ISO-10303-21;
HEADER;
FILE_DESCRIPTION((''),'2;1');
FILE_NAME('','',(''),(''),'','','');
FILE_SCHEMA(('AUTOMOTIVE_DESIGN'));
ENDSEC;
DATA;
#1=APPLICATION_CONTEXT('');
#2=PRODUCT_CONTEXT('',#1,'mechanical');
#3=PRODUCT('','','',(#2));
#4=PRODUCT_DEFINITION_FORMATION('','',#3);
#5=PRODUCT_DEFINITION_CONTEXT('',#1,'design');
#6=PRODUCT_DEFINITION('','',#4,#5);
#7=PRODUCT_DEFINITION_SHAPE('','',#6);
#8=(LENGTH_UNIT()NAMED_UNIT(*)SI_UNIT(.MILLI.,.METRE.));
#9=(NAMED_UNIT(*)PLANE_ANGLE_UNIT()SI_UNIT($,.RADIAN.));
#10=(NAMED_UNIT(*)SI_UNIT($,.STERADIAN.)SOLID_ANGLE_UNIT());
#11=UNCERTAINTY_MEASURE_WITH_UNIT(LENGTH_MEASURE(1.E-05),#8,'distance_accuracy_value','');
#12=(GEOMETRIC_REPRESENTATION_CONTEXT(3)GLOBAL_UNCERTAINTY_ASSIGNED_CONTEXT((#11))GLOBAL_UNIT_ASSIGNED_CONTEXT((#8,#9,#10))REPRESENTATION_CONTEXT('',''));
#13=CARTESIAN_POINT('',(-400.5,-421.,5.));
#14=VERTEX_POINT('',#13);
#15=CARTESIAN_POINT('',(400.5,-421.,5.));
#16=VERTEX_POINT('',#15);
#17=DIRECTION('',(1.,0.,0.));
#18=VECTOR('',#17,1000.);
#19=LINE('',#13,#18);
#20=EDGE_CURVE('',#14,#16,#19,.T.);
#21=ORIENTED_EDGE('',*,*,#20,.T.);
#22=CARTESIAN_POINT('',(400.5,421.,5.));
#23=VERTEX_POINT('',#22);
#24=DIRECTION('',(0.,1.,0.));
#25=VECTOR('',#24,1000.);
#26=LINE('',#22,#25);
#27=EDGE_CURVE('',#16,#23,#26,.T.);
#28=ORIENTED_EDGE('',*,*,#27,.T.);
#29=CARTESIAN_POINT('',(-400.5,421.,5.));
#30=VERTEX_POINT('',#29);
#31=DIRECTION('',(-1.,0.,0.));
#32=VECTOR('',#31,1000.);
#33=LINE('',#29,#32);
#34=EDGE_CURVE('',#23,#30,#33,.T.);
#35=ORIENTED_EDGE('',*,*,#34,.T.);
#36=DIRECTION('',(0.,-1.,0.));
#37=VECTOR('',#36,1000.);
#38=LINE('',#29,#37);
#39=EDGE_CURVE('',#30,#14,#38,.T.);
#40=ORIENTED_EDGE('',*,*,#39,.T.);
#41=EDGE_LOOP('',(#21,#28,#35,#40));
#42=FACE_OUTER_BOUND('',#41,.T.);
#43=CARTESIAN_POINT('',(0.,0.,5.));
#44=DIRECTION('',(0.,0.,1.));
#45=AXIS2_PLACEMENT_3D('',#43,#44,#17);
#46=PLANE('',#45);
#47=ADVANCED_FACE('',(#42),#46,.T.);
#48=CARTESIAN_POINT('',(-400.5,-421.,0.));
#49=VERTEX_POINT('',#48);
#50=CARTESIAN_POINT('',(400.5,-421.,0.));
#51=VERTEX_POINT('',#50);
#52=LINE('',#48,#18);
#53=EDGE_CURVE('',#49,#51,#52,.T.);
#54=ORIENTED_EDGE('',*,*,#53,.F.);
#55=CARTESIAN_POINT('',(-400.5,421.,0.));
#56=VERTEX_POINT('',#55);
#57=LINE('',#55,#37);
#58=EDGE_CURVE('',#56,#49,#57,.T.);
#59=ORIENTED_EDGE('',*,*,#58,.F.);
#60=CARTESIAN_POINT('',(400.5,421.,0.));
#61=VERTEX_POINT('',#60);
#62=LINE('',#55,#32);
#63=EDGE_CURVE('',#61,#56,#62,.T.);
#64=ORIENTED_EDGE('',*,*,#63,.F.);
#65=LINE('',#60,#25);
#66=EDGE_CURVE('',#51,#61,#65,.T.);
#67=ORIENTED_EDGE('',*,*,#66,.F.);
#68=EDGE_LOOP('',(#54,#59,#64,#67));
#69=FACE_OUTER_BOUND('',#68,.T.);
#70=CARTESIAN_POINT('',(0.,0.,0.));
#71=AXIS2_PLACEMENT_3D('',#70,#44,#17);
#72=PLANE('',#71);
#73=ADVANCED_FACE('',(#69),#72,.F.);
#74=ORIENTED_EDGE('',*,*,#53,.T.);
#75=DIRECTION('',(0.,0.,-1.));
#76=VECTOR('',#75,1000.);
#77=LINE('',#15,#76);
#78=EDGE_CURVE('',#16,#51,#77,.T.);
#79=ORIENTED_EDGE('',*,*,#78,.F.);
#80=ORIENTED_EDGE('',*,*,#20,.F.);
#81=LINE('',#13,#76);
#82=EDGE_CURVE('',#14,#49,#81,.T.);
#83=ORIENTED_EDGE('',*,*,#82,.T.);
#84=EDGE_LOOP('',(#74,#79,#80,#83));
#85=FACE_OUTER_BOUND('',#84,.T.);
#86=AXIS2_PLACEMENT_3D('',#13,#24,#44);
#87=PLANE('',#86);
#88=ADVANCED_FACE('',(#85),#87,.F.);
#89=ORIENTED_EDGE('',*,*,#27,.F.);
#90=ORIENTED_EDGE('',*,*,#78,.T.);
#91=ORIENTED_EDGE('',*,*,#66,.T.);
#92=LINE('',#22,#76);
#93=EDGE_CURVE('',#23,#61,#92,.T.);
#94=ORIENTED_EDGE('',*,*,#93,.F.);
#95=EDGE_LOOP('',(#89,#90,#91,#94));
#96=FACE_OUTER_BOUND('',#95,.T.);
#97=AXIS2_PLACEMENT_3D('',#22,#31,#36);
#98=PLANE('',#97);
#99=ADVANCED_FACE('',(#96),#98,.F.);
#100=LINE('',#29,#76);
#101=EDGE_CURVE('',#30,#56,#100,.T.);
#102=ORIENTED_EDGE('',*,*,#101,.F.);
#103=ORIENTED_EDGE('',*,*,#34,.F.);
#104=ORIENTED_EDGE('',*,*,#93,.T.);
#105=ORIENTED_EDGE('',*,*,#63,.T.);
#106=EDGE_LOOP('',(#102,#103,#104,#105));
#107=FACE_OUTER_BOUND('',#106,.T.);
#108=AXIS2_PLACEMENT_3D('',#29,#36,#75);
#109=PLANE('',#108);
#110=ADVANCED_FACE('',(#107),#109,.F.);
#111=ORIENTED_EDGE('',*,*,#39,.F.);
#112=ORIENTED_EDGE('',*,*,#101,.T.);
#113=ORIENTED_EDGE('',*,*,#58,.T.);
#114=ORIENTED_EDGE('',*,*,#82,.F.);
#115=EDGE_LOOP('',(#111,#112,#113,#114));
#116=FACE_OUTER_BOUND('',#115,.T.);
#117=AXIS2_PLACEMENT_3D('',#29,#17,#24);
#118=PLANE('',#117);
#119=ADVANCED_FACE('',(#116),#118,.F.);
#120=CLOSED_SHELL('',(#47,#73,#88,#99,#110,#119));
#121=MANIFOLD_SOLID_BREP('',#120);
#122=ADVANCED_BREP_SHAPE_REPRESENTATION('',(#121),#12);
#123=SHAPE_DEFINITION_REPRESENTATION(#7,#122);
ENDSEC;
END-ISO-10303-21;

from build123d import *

# Parameters (mm, degrees)
SKETCH_1_W      = 801
SKETCH_1_H      = 842
EXTRUDE_1_DEPTH = 5


with BuildPart() as part:
    # 草图1 → 凸台-拉伸1 (new body)
    with BuildSketch(Plane.XY):
        Rectangle(SKETCH_1_W, SKETCH_1_H)
    extrude(amount=EXTRUDE_1_DEPTH)


solid = part.part
